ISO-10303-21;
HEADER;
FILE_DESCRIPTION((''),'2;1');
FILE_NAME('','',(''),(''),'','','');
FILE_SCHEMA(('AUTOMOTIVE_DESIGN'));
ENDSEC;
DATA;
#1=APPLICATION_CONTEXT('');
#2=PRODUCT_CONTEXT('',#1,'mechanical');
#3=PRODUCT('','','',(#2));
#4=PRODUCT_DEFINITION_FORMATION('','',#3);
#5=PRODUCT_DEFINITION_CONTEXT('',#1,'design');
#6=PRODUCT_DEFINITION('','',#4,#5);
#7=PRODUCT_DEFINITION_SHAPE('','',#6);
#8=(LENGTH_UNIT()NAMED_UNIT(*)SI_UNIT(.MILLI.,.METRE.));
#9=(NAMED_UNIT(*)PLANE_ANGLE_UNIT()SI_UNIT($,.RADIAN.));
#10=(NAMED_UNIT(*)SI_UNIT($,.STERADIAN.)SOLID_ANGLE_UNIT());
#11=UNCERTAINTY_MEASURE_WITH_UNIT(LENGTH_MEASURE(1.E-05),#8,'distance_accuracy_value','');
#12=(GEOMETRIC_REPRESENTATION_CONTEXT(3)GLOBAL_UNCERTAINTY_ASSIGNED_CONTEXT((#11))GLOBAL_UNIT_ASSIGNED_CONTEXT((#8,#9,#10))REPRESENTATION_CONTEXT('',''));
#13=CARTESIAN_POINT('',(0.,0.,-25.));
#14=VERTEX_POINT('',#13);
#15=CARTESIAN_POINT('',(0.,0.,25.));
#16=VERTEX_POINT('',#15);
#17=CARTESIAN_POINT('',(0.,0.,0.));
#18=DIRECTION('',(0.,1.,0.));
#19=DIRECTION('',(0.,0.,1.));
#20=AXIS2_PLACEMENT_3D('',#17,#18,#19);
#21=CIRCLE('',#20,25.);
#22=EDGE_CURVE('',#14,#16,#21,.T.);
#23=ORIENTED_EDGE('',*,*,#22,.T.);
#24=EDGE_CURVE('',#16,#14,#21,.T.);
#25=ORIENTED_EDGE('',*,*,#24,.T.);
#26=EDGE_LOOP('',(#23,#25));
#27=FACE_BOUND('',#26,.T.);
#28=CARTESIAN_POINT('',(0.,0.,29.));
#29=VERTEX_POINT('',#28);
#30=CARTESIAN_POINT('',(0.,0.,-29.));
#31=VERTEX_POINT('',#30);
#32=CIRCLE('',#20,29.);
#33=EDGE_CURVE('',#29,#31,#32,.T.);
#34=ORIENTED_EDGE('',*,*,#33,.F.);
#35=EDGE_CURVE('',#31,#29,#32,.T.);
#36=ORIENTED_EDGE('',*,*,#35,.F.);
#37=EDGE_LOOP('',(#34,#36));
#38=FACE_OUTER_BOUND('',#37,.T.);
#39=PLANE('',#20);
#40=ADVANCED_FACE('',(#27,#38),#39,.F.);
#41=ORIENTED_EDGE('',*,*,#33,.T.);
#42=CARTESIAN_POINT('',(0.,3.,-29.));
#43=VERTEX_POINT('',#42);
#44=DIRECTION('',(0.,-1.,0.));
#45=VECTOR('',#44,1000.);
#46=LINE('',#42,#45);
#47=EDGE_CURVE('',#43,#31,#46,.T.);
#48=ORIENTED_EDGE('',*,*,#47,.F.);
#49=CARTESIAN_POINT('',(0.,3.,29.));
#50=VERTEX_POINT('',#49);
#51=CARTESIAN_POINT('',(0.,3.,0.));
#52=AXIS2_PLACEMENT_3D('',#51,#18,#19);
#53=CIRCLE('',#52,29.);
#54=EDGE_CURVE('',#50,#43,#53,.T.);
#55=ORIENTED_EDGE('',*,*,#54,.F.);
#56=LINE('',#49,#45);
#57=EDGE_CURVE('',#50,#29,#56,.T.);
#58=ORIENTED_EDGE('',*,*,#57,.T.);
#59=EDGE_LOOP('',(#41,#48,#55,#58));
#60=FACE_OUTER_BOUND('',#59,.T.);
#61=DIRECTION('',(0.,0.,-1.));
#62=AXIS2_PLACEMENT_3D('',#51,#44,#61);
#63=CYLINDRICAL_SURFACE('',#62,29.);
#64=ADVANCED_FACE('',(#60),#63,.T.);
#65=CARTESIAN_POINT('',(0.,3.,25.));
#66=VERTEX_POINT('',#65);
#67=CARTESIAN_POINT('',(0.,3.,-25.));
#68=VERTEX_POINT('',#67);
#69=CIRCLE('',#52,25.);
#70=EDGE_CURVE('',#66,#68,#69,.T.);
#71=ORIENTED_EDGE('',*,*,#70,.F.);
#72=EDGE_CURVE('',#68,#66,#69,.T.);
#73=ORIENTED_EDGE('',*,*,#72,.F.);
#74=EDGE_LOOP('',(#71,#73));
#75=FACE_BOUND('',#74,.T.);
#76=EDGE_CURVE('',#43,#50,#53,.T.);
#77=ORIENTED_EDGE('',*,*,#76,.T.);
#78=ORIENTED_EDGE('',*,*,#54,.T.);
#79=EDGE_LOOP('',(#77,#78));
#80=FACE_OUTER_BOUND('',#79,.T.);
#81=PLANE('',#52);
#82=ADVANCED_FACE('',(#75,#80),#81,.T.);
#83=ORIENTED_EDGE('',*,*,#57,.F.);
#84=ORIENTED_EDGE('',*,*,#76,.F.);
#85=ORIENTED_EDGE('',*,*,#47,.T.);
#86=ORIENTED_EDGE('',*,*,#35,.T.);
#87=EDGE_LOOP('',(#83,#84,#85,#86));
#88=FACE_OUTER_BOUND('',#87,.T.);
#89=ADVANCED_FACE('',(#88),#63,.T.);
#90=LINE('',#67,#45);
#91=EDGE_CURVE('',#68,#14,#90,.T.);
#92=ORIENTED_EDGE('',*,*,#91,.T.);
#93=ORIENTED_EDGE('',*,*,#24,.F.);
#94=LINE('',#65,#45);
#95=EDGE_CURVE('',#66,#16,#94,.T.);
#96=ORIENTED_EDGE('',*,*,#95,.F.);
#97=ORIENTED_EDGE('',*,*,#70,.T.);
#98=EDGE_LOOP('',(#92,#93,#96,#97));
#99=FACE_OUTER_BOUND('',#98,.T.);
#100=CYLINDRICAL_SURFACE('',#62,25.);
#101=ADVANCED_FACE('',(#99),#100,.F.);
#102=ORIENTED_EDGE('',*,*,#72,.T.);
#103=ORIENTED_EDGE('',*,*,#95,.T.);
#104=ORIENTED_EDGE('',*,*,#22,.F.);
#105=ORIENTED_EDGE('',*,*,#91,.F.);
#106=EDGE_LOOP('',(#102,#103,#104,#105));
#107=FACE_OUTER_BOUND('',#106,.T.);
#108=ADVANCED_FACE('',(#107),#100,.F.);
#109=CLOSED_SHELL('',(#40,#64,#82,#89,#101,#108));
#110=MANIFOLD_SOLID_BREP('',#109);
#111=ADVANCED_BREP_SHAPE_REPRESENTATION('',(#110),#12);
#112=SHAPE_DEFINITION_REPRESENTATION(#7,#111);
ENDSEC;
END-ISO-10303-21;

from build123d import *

# Parameters (mm, degrees)
SKETCH_1_R      = 29
SKETCH_1_R_2    = 25
EXTRUDE_1_DEPTH = 3


with BuildPart() as part:
    # 草图1 → 凸台-拉伸1 (new body)
    with BuildSketch(Plane(origin=(0, 0, 0), x_dir=(1, 0, 0), z_dir=(0, 1, 0))):
        with Locations(Location((0, 0, 0), (0, 0, 270))):
            Circle(SKETCH_1_R)
        with Locations(Location((0, 0, 0), (0, 0, 270))):
            Circle(SKETCH_1_R_2, mode=Mode.SUBTRACT)
    extrude(amount=EXTRUDE_1_DEPTH)


solid = part.part
